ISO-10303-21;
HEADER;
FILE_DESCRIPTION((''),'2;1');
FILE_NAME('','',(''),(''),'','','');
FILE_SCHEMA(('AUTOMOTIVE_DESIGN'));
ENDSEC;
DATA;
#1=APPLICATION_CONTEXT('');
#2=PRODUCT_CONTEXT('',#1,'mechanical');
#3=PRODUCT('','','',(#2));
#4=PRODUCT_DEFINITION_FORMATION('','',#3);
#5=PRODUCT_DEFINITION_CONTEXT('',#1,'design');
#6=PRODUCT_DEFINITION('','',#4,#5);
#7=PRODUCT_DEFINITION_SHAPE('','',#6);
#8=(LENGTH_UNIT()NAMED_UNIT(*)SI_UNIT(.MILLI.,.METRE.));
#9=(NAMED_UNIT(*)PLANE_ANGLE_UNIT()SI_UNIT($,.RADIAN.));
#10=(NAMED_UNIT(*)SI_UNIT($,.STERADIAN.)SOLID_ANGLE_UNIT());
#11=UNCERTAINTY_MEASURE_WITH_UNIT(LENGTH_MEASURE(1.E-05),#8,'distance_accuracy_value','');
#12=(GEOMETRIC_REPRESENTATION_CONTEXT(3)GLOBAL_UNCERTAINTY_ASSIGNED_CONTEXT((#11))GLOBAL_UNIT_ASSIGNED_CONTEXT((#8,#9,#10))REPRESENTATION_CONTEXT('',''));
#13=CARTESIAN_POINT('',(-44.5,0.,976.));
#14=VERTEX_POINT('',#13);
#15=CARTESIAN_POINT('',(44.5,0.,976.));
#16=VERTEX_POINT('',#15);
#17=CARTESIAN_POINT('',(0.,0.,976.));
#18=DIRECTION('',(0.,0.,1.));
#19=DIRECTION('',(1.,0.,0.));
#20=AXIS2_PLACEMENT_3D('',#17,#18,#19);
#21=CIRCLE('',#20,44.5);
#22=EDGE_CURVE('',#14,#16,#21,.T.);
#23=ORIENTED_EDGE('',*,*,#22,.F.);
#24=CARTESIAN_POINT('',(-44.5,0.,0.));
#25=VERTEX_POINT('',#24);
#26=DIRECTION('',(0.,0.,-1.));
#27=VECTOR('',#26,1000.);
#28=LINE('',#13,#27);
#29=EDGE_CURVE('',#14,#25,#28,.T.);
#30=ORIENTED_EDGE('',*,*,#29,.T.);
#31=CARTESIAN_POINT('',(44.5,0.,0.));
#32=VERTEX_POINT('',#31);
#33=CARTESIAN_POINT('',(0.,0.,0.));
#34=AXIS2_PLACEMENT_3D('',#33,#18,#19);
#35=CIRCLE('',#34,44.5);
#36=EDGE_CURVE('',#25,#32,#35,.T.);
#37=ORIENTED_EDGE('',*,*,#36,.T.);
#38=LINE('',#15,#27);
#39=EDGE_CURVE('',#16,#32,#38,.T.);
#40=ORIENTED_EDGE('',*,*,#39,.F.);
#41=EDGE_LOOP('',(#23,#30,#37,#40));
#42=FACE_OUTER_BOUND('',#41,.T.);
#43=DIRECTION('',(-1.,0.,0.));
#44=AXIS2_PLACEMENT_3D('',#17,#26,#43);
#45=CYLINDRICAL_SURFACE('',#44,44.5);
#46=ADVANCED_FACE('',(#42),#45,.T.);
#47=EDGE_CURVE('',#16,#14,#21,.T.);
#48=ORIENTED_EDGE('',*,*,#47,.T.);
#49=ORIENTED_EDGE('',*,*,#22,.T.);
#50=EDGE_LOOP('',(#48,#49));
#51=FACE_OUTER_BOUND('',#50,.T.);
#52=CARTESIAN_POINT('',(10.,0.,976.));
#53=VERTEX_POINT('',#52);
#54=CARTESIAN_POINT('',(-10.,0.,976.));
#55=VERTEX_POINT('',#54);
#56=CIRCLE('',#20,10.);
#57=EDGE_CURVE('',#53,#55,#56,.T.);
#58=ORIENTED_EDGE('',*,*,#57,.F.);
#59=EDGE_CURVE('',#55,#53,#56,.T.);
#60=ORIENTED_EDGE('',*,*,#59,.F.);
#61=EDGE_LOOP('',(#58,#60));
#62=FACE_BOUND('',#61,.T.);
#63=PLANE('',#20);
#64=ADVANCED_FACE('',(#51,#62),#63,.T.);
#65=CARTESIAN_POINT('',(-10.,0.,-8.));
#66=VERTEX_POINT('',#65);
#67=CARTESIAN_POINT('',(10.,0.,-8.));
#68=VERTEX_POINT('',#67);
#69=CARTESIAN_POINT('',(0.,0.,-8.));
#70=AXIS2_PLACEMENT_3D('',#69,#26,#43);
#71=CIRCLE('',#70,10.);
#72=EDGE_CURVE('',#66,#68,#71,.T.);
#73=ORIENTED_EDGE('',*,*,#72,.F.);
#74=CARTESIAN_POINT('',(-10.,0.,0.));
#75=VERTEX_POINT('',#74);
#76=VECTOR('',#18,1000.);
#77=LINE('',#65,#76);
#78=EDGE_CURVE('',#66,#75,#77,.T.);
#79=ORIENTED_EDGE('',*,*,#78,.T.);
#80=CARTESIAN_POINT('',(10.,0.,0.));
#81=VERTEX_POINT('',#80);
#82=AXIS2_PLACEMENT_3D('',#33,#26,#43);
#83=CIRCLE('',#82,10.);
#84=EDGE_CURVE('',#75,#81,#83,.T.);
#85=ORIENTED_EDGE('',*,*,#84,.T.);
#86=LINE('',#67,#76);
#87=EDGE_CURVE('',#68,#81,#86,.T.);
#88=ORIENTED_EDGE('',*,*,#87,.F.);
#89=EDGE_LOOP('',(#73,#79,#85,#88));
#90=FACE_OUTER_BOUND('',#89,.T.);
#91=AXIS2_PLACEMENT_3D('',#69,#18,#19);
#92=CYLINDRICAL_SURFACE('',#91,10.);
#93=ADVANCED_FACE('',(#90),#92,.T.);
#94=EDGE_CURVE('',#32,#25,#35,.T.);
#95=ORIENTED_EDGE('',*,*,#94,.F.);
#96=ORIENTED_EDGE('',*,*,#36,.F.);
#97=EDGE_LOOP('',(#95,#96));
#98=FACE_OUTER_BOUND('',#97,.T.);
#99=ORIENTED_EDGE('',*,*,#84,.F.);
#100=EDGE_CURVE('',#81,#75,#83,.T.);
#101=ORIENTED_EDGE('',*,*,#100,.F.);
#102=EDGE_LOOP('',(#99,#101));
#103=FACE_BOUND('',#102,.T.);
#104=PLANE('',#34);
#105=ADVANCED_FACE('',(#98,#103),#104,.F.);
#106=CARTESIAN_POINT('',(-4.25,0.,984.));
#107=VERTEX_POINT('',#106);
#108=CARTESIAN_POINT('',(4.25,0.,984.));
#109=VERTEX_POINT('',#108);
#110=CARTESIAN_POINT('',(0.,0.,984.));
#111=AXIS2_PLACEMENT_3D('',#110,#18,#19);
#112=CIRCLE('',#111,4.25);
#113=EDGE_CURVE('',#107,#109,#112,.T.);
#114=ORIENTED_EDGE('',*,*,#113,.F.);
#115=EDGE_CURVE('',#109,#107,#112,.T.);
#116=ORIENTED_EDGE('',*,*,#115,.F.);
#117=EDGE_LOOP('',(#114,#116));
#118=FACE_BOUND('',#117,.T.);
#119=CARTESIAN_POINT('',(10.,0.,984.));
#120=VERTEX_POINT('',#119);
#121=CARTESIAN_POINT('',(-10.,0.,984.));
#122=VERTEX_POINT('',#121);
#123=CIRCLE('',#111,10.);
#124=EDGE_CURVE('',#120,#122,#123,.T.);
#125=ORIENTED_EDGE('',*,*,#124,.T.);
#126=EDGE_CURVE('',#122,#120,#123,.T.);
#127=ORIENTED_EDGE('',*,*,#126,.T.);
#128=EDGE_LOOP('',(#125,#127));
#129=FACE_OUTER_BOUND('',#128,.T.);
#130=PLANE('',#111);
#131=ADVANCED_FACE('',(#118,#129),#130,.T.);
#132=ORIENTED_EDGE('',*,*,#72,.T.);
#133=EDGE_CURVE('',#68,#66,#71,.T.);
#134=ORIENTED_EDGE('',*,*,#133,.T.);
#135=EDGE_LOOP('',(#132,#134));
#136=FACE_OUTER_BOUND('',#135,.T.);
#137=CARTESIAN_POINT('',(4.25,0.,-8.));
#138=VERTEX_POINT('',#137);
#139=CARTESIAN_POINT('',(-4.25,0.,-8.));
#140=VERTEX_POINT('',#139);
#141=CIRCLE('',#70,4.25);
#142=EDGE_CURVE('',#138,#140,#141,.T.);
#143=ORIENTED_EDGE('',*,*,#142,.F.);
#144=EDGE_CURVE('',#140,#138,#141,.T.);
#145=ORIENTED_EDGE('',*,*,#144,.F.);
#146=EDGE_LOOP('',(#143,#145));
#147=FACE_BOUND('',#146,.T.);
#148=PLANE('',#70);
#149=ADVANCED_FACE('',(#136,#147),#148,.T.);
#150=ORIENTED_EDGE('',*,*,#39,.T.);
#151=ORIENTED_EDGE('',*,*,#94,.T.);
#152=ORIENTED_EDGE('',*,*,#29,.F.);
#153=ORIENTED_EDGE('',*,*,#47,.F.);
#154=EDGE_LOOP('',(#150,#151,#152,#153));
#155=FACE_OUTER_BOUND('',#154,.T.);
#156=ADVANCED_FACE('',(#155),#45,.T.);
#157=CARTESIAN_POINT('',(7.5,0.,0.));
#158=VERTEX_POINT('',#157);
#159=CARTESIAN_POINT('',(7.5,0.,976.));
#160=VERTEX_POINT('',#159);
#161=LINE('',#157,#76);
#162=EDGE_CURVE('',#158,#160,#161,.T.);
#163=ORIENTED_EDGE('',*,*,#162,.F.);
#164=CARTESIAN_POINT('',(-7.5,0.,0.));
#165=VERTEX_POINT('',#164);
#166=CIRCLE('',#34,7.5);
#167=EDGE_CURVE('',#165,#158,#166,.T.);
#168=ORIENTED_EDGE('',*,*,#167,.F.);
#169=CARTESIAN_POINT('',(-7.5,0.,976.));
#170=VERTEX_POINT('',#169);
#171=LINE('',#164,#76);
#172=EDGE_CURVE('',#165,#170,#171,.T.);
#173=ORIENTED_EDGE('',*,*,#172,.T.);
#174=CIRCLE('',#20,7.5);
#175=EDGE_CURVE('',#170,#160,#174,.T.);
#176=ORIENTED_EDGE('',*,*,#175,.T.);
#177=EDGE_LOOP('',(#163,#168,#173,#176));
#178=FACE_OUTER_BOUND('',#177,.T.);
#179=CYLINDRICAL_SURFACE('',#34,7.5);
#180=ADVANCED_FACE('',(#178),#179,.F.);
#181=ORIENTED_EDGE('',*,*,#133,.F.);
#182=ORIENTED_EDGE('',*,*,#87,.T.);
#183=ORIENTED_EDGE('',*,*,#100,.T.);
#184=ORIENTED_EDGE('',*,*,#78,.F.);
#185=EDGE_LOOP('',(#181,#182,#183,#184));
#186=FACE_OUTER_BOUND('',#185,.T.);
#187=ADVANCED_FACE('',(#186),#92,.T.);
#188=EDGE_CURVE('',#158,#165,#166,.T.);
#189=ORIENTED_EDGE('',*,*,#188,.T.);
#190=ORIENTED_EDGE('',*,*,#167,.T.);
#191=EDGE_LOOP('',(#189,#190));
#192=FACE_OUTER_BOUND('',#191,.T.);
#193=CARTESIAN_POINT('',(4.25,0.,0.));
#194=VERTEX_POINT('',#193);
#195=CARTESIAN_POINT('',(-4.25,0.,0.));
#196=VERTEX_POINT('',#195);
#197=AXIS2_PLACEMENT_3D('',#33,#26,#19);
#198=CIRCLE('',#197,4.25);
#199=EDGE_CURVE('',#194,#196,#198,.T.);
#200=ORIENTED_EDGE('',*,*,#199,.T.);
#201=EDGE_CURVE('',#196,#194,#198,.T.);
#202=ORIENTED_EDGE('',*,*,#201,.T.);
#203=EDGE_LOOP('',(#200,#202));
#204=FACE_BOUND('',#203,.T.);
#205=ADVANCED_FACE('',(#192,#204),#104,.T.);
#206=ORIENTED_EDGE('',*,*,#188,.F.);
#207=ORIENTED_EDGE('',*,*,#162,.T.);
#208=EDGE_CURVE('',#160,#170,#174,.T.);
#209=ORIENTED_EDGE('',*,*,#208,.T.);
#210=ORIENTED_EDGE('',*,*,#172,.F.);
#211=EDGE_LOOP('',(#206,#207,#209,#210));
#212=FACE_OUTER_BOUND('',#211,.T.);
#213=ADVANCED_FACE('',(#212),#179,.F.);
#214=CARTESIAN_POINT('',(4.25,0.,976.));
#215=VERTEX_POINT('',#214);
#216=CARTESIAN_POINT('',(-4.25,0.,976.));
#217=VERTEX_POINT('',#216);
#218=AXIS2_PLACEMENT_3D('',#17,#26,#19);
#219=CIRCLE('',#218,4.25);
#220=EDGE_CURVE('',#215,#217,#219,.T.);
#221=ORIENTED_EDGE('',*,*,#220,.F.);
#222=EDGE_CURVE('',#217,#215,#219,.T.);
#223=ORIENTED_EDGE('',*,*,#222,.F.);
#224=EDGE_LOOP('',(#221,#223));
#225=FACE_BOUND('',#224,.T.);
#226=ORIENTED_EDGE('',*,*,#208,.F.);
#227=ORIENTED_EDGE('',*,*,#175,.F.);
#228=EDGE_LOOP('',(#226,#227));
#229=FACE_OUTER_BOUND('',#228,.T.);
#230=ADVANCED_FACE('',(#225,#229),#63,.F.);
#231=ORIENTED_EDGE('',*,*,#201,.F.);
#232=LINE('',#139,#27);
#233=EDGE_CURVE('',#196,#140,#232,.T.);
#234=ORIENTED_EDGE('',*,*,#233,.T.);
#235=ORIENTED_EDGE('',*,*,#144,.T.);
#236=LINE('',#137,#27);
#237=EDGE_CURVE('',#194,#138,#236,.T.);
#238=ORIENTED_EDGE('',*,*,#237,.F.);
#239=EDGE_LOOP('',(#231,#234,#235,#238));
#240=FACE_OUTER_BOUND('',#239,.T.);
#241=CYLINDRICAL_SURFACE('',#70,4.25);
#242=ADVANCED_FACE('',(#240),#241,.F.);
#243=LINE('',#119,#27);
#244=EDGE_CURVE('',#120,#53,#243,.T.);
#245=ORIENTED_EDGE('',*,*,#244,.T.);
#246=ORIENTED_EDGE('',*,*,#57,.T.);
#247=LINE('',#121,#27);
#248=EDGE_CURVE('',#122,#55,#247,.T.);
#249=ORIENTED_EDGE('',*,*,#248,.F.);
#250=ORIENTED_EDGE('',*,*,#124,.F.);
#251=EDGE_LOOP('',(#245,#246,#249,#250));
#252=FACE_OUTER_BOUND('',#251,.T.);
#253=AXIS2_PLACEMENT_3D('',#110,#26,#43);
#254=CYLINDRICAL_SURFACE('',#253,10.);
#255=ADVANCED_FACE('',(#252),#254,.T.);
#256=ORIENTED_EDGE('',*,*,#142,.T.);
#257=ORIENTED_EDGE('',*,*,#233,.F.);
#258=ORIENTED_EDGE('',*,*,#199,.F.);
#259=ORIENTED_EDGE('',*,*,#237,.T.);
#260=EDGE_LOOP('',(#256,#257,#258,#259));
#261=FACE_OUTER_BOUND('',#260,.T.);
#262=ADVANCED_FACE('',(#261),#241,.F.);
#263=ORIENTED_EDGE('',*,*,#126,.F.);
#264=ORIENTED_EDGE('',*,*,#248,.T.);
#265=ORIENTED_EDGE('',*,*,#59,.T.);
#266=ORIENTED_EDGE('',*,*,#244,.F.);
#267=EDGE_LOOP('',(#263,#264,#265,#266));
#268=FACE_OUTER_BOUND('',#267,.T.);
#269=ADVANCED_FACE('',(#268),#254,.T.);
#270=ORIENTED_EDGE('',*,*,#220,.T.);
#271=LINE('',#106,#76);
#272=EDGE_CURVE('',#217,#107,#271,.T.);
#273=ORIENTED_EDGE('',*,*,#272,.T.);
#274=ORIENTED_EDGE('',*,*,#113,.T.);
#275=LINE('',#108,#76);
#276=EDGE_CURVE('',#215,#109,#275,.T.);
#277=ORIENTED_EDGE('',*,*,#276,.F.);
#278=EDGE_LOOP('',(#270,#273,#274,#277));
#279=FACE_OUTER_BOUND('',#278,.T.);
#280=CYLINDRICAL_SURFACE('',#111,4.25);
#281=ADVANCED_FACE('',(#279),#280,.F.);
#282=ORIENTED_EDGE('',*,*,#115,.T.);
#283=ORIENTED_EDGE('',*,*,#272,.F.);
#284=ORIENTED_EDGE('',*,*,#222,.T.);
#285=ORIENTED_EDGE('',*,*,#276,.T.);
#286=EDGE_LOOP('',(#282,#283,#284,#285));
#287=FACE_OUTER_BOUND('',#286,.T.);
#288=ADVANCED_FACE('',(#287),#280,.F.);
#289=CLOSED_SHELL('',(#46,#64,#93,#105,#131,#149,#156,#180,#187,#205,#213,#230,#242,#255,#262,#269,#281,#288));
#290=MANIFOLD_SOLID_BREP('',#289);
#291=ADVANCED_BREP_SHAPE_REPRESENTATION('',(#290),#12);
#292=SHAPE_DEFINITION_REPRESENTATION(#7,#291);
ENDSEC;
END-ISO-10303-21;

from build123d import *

# Parameters (mm, degrees)
SKETCH_1_R              = 44.5
EXTRUDE_1_DEPTH         = 976
SKETCH_2_R              = 10
EXTRUDE_2_DEPTH         = 8
EXTRUDE_START           = 8
SKETCH_3_R              = 10
EXTRUDE_3_DEPTH         = 8
HOLE_WIZARD_M10_1_D     = 8.5
HOLE_WIZARD_M10_1_DEPTH = 22.5
HOLE_WIZARD_M10_1_TIP   = 2.553657631
HOLE_WIZARD_M10_2_D     = 8.5
HOLE_WIZARD_M10_2_DEPTH = 22.5
HOLE_WIZARD_M10_2_TIP   = 2.553657631
SKETCH_11_R             = 7.5
CUT_EXTRUDE_1_DEPTH     = 488


with BuildPart() as part:
    # 草图1 → 凸台-拉伸1 (new body)
    with BuildSketch(Plane.XY):
        with Locations(Location((0, 0, 0), (0, 0, 180))):
            Circle(SKETCH_1_R)
    extrude(amount=EXTRUDE_1_DEPTH)

    # 草图2 → 凸台-拉伸2 (add)
    with BuildSketch(Plane.XY.offset(976)):
        Circle(SKETCH_2_R)
    extrude(amount=EXTRUDE_2_DEPTH)

    # 草图3 → 凸台-拉伸3 (add)
    with BuildSketch(Plane(origin=(0, 0, 0), x_dir=(-1, 0, 0), z_dir=(0, 0, -1)).offset(EXTRUDE_START)):
        with Locations(Location((0, 0, 0), (0, 0, 180))):
            Circle(SKETCH_3_R)
    extrude(amount=-EXTRUDE_3_DEPTH)

    # M10 螺纹孔1
    with Locations(Plane(origin=(0, 0, -8), x_dir=(-1, 0, 0), z_dir=(0, 0, -1))):
        with Locations((0, 0)):
            Hole(HOLE_WIZARD_M10_1_D / 2, depth=HOLE_WIZARD_M10_1_DEPTH)
            with Locations((0, 0, -(HOLE_WIZARD_M10_1_DEPTH + HOLE_WIZARD_M10_1_TIP / 2))):  # 118° drill point
                Cone(0, HOLE_WIZARD_M10_1_D / 2, HOLE_WIZARD_M10_1_TIP, mode=Mode.SUBTRACT)

    # M10 螺纹孔2
    with Locations(Plane.XY.offset(984)):
        with Locations((0, 0)):
            Hole(HOLE_WIZARD_M10_2_D / 2, depth=HOLE_WIZARD_M10_2_DEPTH)
            with Locations((0, 0, -(HOLE_WIZARD_M10_2_DEPTH + HOLE_WIZARD_M10_2_TIP / 2))):  # 118° drill point
                Cone(0, HOLE_WIZARD_M10_2_D / 2, HOLE_WIZARD_M10_2_TIP, mode=Mode.SUBTRACT)

    # 草图11 → 切除-拉伸1 (cut, symmetric)
    with BuildSketch(Plane.XY.offset(488)):
        Circle(SKETCH_11_R)
    extrude(amount=CUT_EXTRUDE_1_DEPTH, both=True, mode=Mode.SUBTRACT)


solid = part.part
